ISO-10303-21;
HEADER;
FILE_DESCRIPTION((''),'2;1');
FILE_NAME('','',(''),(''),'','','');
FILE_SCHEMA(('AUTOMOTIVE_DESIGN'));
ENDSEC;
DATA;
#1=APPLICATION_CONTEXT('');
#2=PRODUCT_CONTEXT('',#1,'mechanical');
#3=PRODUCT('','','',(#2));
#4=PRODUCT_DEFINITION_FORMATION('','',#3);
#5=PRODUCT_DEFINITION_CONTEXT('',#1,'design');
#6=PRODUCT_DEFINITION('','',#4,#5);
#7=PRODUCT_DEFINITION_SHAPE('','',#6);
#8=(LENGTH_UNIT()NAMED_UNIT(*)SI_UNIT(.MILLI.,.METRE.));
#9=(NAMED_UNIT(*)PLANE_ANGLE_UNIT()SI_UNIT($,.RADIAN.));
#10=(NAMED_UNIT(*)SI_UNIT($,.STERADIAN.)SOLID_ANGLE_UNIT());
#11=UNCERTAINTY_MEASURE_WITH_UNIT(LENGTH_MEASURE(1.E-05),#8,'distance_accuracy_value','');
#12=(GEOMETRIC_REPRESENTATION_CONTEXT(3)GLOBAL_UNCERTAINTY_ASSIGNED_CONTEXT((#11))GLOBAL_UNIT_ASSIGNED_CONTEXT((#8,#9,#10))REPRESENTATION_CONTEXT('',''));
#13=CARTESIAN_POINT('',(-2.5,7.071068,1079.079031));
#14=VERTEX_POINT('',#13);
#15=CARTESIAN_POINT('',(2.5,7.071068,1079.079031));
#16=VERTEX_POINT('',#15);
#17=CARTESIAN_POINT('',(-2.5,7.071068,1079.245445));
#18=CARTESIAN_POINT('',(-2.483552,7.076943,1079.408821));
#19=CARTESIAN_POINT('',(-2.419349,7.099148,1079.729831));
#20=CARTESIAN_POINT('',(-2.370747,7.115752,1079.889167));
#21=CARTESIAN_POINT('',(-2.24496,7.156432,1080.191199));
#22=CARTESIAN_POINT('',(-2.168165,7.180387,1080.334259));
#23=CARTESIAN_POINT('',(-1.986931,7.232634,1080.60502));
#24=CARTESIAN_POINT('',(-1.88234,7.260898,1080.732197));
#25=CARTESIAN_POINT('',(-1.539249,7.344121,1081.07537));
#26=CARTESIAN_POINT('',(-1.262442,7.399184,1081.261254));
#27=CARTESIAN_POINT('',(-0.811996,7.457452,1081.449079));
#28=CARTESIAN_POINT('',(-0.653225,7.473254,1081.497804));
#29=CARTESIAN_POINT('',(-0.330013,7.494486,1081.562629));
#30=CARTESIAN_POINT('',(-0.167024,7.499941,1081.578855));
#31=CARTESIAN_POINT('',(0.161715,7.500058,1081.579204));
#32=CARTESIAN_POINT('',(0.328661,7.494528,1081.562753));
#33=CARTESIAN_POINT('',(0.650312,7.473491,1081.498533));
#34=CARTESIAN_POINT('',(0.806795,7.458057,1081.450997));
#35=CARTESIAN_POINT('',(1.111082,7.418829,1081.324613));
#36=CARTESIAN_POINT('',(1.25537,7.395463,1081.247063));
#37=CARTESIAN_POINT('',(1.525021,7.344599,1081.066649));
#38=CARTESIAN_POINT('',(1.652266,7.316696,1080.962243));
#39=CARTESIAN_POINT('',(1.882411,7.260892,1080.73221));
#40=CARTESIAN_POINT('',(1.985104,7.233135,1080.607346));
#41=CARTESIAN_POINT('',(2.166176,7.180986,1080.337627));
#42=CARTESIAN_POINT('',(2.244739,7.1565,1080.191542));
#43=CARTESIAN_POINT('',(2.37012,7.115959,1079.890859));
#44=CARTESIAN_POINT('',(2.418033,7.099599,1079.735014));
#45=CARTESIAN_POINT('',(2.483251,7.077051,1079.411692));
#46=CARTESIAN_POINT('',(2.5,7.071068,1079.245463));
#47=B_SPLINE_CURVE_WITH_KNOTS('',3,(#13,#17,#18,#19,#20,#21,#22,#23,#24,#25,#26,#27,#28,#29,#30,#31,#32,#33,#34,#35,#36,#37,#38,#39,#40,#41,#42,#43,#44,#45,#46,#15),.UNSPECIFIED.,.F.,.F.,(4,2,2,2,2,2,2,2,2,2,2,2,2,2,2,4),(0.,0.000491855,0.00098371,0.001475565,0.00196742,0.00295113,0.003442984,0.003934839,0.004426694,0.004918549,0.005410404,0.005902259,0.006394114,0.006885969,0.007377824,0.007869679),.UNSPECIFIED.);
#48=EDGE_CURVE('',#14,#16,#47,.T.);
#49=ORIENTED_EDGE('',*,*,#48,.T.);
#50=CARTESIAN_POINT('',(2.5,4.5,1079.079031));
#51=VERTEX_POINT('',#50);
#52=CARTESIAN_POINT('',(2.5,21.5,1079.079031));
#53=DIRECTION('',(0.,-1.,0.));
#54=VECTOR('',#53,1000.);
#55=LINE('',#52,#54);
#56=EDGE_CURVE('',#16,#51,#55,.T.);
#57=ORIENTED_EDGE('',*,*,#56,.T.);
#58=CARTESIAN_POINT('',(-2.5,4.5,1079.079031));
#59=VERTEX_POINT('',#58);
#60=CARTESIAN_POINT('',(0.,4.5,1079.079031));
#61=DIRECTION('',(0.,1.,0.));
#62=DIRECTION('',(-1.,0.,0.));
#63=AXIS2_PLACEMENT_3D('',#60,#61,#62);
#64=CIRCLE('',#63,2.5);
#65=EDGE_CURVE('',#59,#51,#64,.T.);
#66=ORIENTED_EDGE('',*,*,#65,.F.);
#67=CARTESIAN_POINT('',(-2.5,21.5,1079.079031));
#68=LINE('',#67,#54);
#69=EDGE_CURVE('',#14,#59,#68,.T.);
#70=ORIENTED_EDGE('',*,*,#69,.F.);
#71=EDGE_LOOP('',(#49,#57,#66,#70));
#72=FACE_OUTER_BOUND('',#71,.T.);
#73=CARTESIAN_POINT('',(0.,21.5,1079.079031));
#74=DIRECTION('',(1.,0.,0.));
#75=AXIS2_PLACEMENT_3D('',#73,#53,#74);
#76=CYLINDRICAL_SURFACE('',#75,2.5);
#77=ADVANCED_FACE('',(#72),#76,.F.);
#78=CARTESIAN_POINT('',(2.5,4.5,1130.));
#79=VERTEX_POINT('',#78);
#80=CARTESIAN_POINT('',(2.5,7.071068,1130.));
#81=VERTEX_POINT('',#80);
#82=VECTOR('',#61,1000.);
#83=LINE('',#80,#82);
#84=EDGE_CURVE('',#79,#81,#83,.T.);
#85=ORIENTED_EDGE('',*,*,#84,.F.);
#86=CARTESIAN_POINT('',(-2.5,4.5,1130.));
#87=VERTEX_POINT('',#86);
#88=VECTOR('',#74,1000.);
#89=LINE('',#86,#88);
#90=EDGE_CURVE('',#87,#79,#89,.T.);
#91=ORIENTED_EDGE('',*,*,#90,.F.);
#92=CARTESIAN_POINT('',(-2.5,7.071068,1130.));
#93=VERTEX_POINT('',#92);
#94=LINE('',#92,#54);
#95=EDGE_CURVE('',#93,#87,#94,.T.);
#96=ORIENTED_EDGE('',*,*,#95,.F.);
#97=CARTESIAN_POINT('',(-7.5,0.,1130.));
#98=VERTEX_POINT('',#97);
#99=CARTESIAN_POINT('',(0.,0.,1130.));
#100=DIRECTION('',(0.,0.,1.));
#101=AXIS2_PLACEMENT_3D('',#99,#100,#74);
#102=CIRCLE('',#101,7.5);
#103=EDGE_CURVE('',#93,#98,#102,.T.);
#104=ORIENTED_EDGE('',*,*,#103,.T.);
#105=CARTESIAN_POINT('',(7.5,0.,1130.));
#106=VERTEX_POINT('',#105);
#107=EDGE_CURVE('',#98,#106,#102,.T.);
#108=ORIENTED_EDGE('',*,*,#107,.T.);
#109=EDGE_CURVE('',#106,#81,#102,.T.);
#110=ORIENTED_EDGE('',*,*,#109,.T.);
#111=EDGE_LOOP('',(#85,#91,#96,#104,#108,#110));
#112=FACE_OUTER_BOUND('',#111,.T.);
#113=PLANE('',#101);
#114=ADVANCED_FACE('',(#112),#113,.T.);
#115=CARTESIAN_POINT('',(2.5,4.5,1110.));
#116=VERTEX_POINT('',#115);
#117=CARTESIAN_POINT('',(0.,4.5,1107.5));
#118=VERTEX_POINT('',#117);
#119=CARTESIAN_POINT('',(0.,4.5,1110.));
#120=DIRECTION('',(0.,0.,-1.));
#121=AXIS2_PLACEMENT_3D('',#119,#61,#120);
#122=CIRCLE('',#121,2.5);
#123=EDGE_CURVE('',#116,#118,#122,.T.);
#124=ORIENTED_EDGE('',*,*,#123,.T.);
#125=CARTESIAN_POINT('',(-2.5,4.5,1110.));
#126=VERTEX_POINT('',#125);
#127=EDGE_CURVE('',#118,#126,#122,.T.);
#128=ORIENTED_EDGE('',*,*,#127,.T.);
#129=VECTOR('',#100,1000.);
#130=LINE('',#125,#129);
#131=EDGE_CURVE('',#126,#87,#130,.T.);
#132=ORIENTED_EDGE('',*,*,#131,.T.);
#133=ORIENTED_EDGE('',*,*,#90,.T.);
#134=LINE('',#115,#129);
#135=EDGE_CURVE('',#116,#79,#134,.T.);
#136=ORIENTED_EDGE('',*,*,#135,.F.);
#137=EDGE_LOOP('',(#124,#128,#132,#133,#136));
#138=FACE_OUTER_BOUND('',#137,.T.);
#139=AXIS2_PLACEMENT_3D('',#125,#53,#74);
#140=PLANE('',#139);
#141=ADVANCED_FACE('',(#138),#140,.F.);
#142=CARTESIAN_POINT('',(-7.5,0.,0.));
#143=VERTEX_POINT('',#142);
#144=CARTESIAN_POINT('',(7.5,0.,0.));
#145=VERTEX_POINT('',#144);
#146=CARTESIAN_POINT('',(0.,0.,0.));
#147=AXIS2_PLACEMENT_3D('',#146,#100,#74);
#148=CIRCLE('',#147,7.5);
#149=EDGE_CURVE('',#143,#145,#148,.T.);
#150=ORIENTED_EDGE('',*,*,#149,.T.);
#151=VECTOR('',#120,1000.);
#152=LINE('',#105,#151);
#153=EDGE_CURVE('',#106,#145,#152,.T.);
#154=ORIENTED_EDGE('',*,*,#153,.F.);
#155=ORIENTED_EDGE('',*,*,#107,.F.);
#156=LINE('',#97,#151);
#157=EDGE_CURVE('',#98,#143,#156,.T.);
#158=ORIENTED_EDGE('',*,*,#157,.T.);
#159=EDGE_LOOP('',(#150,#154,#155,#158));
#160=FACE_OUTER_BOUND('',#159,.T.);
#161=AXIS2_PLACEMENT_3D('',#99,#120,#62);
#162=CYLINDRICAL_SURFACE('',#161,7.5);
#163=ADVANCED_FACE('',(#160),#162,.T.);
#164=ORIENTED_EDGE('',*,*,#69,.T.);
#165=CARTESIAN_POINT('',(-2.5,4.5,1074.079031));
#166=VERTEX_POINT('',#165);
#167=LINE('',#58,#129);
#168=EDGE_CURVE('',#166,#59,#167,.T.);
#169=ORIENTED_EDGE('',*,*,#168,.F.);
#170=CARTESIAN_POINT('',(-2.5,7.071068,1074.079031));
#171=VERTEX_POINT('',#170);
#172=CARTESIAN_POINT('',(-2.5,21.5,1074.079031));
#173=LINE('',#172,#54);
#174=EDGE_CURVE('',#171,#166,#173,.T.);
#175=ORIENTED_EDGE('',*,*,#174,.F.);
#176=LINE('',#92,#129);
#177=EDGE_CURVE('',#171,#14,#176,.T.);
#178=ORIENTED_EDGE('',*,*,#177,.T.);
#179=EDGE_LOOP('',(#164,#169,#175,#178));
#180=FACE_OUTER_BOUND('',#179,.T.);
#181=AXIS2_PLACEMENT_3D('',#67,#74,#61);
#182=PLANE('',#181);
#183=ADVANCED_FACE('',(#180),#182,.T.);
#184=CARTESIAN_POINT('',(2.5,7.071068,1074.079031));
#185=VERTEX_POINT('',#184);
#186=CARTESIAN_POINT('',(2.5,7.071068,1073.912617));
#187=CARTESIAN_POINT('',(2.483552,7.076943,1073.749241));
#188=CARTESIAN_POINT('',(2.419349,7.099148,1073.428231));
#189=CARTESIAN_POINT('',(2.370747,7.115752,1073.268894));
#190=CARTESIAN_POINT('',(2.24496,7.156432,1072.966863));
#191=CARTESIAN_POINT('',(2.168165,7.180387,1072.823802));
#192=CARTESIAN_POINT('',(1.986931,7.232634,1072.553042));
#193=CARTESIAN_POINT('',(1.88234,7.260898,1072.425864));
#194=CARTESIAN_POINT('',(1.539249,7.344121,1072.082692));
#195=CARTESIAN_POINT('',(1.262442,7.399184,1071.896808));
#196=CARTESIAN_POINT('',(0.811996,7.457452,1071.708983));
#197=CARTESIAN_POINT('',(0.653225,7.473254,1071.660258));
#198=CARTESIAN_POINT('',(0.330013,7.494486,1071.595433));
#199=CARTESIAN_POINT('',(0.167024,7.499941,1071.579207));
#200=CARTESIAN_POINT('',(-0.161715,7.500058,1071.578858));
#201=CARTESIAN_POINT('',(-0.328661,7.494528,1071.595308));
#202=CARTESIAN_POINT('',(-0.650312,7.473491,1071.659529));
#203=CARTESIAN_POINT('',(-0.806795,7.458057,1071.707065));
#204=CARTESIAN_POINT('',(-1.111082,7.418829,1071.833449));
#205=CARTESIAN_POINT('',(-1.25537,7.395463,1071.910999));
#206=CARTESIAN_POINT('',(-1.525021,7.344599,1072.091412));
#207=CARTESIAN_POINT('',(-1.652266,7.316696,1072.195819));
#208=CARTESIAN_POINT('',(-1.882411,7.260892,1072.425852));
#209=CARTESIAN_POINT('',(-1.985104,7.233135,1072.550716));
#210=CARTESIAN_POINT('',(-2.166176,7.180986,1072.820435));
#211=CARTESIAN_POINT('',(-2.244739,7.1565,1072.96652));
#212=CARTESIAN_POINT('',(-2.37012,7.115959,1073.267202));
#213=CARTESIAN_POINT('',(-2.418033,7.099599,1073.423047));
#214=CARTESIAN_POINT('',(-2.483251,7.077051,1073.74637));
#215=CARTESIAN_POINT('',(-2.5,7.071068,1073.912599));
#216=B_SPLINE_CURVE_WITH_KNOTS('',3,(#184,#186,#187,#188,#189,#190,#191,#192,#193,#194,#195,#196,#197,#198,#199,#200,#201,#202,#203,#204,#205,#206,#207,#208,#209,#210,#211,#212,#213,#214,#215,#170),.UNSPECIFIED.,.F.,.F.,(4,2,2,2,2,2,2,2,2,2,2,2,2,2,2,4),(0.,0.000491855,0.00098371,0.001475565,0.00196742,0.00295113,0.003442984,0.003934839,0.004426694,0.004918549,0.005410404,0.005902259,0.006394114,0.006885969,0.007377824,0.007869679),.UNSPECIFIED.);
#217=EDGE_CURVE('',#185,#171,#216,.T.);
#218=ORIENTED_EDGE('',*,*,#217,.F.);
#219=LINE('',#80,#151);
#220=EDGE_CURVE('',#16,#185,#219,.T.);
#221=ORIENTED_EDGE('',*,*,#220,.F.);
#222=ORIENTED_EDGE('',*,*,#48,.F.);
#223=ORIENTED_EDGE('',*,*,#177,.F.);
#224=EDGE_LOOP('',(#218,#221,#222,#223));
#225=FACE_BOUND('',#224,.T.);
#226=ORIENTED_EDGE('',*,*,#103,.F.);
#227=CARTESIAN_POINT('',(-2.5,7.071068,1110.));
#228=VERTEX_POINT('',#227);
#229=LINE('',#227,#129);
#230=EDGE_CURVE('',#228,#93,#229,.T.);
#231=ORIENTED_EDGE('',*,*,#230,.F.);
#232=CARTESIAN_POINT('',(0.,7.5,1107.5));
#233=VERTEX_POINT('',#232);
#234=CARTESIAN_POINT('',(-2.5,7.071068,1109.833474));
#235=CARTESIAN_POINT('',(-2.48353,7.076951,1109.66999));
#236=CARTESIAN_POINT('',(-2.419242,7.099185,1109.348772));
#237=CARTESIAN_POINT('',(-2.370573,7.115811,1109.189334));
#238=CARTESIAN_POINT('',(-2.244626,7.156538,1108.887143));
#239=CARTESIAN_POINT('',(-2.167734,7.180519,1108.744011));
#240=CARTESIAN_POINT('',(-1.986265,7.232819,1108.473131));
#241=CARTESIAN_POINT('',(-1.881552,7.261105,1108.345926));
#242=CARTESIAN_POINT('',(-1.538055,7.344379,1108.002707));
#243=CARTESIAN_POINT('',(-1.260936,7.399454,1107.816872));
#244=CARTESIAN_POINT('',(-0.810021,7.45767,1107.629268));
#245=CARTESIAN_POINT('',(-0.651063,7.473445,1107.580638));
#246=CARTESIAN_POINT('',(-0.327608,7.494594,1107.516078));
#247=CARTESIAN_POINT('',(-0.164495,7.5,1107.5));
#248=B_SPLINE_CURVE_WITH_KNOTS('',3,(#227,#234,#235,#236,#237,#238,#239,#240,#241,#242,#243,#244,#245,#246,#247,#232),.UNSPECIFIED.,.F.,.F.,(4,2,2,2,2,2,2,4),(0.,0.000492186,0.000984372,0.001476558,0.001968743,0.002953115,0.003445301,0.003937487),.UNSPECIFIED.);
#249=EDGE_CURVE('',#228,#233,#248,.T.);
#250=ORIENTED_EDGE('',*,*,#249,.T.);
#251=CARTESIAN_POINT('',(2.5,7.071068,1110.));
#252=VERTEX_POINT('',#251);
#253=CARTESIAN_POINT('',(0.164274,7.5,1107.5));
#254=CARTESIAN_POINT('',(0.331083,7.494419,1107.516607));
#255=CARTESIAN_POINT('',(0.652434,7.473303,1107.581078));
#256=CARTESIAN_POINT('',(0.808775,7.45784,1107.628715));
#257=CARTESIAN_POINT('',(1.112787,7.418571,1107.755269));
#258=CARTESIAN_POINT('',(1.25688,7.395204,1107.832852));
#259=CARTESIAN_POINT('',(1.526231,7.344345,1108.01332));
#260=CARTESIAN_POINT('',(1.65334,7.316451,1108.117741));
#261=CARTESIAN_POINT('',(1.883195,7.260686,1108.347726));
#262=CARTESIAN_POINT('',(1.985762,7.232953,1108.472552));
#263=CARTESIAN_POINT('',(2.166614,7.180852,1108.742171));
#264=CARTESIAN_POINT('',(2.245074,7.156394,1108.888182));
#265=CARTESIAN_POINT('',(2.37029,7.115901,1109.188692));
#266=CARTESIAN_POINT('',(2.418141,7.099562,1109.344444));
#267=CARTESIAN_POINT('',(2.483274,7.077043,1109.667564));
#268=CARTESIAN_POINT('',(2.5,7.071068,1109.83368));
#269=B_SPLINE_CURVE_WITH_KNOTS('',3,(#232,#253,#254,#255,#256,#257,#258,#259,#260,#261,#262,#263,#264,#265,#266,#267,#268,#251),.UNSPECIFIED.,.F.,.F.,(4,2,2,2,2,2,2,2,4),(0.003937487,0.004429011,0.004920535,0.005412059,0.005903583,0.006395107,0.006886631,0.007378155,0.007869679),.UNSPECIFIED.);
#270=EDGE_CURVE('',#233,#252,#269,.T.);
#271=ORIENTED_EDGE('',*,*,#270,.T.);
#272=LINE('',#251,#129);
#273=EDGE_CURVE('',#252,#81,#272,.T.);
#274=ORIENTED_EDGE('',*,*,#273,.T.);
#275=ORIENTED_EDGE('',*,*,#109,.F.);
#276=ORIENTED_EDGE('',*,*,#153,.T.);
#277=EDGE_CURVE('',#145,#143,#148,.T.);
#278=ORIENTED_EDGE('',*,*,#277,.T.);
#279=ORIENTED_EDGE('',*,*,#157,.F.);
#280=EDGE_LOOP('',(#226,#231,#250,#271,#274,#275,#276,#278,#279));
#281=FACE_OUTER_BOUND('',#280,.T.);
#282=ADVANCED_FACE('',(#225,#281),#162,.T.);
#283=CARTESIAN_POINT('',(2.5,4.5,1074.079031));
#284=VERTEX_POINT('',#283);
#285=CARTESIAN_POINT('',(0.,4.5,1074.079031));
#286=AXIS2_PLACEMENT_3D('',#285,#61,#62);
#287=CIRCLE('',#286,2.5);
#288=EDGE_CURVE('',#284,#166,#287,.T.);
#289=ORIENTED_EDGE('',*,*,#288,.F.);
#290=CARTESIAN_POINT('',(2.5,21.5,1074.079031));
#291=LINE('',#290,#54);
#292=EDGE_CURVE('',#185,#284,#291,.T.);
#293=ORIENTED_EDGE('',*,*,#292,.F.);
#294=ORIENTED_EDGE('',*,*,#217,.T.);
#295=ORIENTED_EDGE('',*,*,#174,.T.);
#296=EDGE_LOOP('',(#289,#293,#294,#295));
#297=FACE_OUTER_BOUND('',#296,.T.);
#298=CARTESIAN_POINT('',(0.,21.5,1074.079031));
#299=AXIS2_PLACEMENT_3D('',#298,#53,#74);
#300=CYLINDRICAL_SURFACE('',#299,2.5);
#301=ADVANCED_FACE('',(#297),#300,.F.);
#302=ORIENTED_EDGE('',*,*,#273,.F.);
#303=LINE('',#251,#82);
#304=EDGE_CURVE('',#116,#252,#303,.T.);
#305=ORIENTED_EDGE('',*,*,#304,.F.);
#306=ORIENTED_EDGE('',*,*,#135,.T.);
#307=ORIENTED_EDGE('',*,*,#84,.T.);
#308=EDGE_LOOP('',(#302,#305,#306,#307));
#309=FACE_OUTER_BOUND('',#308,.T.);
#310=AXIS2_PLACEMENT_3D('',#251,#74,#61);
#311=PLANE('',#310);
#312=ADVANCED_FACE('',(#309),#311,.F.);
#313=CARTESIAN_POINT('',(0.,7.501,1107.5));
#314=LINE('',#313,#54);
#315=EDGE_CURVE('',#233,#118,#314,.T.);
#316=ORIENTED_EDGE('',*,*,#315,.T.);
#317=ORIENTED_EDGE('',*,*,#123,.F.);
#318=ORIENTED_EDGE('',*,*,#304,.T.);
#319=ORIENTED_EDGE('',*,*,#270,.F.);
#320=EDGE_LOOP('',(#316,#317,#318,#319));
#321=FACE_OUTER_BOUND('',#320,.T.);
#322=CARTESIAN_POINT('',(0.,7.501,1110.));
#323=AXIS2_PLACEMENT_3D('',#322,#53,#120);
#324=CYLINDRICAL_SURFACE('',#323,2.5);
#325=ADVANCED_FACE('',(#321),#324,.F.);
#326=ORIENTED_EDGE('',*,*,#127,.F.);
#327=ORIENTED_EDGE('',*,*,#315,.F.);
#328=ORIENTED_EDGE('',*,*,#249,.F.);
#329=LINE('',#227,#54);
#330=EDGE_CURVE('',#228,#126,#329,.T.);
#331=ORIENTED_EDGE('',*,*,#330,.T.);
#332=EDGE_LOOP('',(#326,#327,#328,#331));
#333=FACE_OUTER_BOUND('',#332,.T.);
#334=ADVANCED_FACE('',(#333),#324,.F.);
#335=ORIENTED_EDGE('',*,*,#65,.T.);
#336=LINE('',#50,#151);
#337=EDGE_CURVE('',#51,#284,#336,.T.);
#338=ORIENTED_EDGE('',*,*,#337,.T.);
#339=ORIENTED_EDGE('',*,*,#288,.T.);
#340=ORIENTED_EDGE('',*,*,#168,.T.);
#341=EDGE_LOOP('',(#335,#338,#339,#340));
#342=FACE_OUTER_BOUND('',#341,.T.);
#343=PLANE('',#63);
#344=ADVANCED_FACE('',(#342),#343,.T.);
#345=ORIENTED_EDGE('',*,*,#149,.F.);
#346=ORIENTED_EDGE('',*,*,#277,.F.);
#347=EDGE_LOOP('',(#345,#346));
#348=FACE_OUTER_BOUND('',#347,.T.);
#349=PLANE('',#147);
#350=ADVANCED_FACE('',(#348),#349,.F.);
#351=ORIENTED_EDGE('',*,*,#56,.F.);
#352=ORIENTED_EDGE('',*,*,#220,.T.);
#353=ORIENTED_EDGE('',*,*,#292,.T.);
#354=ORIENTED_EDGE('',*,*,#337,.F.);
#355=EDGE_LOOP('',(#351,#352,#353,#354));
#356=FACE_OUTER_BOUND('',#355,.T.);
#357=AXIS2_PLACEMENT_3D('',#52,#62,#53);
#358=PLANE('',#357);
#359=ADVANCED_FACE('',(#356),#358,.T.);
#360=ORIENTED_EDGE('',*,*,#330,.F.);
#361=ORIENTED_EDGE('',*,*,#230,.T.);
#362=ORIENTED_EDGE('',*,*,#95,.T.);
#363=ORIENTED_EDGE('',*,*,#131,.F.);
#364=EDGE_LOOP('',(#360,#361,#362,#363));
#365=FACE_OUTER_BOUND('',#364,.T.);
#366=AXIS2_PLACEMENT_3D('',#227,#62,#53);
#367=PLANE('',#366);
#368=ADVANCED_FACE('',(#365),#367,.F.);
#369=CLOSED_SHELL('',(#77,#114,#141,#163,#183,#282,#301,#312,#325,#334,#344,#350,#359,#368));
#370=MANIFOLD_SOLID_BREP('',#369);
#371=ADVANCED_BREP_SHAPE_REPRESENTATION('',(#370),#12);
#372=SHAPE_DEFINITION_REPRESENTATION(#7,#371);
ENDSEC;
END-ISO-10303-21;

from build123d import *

# Parameters (mm, degrees)
SKETCH_1_R               = 7.5
EXTRUDE_1_DEPTH          = 1130
CUT_EXTRUDE_START        = -20
CUT_EXTRUDE_1_DEPTH      = 20
CUT_EXTRUDE_2_REACH      = 1132.089
CUT_EXTRUDE_2_END_RADIUS = 7.5
CUT_EXTRUDE_3_DEPTH      = 17


with BuildPart() as part:
    # 草图1 → 凸台-拉伸1 (new body)
    with BuildSketch(Plane.XY):
        Circle(SKETCH_1_R)
    extrude(amount=EXTRUDE_1_DEPTH)

    # 草图2 → 切除-拉伸1 (cut)
    with BuildSketch(Plane.XY.offset(1130).offset(CUT_EXTRUDE_START)):
        with BuildLine():
            Line((-2.5, 7.071067812), (-2.5, 4.5))
            Line((-2.5, 4.5), (2.5, 4.5))
            Line((2.5, 4.5), (2.5, 7.071067812))
            ThreePointArc((2.5, 7.071067812), (0, 7.5), (-2.5, 7.071067812))
        make_face()
    extrude(amount=CUT_EXTRUDE_1_DEPTH, mode=Mode.SUBTRACT)

    # 切除-拉伸2: up to this cylinder (the profile starts inside it)
    cut_extrude_2_end = Plane(origin=(0, 0, 1108.938967), z_dir=(0, 0, -1)) * Cylinder(CUT_EXTRUDE_2_END_RADIUS, 2280.178, mode=Mode.PRIVATE)
    # 草图3 → 切除-拉伸2 (cut, up to the surface)
    with BuildSketch(Plane(origin=(0, 4.5, 0), x_dir=(1, 0, 0), z_dir=(0, 1, 0)), mode=Mode.PRIVATE) as cut_extrude_2_sk1:
        with BuildLine():
            Line((-2.5, -1110), (2.5, -1110))
            ThreePointArc((2.5, -1110), (0, -1107.5), (-2.5, -1110))
        make_face()
    cut_extrude_2_tool1 = extrude(cut_extrude_2_sk1.sketch, amount=CUT_EXTRUDE_2_REACH, mode=Mode.PRIVATE) & cut_extrude_2_end
    add(cut_extrude_2_tool1.solids().sort_by_distance((0, 4.5, 1108.938967))[0], mode=Mode.SUBTRACT)

    # 草图5 → 切除-拉伸3 (cut)
    with BuildSketch(Plane(origin=(0, 4.5, 0), x_dir=(1, 0, 0), z_dir=(0, 1, 0))):
        with BuildLine():
            Line((-2.5, -1079.079030824), (-2.5, -1074.079030824))
            ThreePointArc((-2.5, -1074.079030824), (0, -1071.579030824), (2.5, -1074.079030824))
            Line((2.5, -1074.079030824), (2.5, -1079.079030824))
            ThreePointArc((2.5, -1079.079030824), (0, -1081.579030824), (-2.5, -1079.079030824))
        make_face()
    extrude(amount=CUT_EXTRUDE_3_DEPTH, mode=Mode.SUBTRACT)


solid = part.part
